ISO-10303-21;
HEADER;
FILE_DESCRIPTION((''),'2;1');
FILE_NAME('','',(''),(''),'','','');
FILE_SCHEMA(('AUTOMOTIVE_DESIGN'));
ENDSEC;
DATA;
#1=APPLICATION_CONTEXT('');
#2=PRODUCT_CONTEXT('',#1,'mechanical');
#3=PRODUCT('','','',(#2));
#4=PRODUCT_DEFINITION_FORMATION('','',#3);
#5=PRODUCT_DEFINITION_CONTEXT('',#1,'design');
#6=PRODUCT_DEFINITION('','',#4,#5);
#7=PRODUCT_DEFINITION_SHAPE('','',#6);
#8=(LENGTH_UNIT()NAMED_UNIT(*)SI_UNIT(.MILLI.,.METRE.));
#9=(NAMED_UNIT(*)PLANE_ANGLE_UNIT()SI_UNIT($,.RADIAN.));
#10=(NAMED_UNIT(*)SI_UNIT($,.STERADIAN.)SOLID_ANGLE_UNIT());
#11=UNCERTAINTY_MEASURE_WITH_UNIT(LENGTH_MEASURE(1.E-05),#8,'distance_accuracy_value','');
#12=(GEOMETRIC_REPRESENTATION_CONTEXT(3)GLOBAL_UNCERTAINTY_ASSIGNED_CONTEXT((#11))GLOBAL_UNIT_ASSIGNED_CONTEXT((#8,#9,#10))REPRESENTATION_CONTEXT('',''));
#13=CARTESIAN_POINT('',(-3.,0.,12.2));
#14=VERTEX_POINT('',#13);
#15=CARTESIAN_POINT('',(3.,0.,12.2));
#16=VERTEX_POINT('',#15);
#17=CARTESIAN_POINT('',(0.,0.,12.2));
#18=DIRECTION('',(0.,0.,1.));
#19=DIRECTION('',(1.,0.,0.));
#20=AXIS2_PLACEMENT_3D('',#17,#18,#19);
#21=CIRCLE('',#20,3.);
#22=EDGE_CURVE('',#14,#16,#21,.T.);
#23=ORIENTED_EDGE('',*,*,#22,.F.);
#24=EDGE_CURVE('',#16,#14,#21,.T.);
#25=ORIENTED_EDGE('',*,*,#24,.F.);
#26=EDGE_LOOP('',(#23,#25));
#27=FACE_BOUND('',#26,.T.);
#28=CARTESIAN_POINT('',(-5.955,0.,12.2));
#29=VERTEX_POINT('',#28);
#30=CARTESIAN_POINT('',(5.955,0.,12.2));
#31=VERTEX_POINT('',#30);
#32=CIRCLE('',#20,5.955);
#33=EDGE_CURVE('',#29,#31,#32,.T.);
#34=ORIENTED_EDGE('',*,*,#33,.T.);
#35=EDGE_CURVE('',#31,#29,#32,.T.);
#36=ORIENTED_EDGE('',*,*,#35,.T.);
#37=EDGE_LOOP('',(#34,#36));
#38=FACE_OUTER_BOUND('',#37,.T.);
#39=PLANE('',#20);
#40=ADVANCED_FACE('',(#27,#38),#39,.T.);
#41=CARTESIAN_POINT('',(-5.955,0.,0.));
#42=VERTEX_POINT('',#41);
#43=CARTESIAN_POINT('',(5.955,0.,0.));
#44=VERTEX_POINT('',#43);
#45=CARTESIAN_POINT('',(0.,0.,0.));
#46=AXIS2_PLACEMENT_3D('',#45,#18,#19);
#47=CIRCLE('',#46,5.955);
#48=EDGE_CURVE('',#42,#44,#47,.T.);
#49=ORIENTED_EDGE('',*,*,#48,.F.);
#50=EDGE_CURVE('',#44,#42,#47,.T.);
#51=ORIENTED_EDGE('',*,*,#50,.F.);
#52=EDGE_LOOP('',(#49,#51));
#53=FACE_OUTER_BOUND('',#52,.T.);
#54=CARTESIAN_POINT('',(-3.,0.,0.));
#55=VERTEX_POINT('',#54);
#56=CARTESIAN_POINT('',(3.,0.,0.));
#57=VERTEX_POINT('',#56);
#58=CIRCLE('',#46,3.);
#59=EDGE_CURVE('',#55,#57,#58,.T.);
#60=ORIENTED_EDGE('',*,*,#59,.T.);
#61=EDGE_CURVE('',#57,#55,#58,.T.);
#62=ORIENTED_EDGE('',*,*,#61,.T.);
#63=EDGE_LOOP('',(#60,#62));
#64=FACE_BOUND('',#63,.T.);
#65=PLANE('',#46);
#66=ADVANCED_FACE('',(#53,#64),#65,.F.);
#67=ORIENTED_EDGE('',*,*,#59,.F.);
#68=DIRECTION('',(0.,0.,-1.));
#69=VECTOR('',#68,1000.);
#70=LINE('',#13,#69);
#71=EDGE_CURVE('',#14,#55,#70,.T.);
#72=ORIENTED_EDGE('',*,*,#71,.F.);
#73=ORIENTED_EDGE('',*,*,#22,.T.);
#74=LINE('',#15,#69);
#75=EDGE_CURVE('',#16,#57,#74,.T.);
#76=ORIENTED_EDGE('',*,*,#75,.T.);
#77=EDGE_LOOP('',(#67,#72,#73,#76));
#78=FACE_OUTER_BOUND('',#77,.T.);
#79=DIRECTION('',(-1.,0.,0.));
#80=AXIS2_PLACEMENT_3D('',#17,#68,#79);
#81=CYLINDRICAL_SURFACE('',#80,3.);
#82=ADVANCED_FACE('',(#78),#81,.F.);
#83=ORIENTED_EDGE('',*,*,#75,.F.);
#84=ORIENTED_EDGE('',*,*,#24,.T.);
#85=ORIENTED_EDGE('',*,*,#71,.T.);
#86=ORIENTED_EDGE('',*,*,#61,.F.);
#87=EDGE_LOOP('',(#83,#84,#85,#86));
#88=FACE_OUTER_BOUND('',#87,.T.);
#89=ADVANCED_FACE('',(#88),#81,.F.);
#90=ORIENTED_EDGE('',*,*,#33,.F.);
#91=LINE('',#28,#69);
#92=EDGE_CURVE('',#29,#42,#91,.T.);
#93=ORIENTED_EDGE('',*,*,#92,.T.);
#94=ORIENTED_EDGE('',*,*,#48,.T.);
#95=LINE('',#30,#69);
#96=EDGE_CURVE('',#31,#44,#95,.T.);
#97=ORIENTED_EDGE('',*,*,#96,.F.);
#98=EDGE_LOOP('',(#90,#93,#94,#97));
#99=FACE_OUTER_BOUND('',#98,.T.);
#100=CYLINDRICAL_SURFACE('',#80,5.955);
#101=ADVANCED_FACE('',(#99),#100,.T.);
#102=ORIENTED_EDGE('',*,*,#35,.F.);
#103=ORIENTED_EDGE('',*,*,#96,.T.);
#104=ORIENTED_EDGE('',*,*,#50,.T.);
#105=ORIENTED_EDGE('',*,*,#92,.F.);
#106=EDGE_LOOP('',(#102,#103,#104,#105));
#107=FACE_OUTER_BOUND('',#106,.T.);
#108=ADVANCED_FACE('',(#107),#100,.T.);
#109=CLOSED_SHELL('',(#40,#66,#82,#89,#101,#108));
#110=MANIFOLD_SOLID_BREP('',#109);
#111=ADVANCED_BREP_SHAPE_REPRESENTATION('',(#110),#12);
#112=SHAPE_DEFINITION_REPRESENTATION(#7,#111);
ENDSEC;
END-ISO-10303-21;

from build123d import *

# Parameters (mm, degrees)
SKETCH1_R           = 5.955
SKETCH1_R_2         = 3
BOSS_EXTRUDE1_DEPTH = 12.2


with BuildPart() as part:
    # Sketch1 → Boss-Extrude1 (new body)
    with BuildSketch(Plane.XY):
        Circle(SKETCH1_R)
        Circle(SKETCH1_R_2, mode=Mode.SUBTRACT)
    extrude(amount=BOSS_EXTRUDE1_DEPTH)


solid = part.part
